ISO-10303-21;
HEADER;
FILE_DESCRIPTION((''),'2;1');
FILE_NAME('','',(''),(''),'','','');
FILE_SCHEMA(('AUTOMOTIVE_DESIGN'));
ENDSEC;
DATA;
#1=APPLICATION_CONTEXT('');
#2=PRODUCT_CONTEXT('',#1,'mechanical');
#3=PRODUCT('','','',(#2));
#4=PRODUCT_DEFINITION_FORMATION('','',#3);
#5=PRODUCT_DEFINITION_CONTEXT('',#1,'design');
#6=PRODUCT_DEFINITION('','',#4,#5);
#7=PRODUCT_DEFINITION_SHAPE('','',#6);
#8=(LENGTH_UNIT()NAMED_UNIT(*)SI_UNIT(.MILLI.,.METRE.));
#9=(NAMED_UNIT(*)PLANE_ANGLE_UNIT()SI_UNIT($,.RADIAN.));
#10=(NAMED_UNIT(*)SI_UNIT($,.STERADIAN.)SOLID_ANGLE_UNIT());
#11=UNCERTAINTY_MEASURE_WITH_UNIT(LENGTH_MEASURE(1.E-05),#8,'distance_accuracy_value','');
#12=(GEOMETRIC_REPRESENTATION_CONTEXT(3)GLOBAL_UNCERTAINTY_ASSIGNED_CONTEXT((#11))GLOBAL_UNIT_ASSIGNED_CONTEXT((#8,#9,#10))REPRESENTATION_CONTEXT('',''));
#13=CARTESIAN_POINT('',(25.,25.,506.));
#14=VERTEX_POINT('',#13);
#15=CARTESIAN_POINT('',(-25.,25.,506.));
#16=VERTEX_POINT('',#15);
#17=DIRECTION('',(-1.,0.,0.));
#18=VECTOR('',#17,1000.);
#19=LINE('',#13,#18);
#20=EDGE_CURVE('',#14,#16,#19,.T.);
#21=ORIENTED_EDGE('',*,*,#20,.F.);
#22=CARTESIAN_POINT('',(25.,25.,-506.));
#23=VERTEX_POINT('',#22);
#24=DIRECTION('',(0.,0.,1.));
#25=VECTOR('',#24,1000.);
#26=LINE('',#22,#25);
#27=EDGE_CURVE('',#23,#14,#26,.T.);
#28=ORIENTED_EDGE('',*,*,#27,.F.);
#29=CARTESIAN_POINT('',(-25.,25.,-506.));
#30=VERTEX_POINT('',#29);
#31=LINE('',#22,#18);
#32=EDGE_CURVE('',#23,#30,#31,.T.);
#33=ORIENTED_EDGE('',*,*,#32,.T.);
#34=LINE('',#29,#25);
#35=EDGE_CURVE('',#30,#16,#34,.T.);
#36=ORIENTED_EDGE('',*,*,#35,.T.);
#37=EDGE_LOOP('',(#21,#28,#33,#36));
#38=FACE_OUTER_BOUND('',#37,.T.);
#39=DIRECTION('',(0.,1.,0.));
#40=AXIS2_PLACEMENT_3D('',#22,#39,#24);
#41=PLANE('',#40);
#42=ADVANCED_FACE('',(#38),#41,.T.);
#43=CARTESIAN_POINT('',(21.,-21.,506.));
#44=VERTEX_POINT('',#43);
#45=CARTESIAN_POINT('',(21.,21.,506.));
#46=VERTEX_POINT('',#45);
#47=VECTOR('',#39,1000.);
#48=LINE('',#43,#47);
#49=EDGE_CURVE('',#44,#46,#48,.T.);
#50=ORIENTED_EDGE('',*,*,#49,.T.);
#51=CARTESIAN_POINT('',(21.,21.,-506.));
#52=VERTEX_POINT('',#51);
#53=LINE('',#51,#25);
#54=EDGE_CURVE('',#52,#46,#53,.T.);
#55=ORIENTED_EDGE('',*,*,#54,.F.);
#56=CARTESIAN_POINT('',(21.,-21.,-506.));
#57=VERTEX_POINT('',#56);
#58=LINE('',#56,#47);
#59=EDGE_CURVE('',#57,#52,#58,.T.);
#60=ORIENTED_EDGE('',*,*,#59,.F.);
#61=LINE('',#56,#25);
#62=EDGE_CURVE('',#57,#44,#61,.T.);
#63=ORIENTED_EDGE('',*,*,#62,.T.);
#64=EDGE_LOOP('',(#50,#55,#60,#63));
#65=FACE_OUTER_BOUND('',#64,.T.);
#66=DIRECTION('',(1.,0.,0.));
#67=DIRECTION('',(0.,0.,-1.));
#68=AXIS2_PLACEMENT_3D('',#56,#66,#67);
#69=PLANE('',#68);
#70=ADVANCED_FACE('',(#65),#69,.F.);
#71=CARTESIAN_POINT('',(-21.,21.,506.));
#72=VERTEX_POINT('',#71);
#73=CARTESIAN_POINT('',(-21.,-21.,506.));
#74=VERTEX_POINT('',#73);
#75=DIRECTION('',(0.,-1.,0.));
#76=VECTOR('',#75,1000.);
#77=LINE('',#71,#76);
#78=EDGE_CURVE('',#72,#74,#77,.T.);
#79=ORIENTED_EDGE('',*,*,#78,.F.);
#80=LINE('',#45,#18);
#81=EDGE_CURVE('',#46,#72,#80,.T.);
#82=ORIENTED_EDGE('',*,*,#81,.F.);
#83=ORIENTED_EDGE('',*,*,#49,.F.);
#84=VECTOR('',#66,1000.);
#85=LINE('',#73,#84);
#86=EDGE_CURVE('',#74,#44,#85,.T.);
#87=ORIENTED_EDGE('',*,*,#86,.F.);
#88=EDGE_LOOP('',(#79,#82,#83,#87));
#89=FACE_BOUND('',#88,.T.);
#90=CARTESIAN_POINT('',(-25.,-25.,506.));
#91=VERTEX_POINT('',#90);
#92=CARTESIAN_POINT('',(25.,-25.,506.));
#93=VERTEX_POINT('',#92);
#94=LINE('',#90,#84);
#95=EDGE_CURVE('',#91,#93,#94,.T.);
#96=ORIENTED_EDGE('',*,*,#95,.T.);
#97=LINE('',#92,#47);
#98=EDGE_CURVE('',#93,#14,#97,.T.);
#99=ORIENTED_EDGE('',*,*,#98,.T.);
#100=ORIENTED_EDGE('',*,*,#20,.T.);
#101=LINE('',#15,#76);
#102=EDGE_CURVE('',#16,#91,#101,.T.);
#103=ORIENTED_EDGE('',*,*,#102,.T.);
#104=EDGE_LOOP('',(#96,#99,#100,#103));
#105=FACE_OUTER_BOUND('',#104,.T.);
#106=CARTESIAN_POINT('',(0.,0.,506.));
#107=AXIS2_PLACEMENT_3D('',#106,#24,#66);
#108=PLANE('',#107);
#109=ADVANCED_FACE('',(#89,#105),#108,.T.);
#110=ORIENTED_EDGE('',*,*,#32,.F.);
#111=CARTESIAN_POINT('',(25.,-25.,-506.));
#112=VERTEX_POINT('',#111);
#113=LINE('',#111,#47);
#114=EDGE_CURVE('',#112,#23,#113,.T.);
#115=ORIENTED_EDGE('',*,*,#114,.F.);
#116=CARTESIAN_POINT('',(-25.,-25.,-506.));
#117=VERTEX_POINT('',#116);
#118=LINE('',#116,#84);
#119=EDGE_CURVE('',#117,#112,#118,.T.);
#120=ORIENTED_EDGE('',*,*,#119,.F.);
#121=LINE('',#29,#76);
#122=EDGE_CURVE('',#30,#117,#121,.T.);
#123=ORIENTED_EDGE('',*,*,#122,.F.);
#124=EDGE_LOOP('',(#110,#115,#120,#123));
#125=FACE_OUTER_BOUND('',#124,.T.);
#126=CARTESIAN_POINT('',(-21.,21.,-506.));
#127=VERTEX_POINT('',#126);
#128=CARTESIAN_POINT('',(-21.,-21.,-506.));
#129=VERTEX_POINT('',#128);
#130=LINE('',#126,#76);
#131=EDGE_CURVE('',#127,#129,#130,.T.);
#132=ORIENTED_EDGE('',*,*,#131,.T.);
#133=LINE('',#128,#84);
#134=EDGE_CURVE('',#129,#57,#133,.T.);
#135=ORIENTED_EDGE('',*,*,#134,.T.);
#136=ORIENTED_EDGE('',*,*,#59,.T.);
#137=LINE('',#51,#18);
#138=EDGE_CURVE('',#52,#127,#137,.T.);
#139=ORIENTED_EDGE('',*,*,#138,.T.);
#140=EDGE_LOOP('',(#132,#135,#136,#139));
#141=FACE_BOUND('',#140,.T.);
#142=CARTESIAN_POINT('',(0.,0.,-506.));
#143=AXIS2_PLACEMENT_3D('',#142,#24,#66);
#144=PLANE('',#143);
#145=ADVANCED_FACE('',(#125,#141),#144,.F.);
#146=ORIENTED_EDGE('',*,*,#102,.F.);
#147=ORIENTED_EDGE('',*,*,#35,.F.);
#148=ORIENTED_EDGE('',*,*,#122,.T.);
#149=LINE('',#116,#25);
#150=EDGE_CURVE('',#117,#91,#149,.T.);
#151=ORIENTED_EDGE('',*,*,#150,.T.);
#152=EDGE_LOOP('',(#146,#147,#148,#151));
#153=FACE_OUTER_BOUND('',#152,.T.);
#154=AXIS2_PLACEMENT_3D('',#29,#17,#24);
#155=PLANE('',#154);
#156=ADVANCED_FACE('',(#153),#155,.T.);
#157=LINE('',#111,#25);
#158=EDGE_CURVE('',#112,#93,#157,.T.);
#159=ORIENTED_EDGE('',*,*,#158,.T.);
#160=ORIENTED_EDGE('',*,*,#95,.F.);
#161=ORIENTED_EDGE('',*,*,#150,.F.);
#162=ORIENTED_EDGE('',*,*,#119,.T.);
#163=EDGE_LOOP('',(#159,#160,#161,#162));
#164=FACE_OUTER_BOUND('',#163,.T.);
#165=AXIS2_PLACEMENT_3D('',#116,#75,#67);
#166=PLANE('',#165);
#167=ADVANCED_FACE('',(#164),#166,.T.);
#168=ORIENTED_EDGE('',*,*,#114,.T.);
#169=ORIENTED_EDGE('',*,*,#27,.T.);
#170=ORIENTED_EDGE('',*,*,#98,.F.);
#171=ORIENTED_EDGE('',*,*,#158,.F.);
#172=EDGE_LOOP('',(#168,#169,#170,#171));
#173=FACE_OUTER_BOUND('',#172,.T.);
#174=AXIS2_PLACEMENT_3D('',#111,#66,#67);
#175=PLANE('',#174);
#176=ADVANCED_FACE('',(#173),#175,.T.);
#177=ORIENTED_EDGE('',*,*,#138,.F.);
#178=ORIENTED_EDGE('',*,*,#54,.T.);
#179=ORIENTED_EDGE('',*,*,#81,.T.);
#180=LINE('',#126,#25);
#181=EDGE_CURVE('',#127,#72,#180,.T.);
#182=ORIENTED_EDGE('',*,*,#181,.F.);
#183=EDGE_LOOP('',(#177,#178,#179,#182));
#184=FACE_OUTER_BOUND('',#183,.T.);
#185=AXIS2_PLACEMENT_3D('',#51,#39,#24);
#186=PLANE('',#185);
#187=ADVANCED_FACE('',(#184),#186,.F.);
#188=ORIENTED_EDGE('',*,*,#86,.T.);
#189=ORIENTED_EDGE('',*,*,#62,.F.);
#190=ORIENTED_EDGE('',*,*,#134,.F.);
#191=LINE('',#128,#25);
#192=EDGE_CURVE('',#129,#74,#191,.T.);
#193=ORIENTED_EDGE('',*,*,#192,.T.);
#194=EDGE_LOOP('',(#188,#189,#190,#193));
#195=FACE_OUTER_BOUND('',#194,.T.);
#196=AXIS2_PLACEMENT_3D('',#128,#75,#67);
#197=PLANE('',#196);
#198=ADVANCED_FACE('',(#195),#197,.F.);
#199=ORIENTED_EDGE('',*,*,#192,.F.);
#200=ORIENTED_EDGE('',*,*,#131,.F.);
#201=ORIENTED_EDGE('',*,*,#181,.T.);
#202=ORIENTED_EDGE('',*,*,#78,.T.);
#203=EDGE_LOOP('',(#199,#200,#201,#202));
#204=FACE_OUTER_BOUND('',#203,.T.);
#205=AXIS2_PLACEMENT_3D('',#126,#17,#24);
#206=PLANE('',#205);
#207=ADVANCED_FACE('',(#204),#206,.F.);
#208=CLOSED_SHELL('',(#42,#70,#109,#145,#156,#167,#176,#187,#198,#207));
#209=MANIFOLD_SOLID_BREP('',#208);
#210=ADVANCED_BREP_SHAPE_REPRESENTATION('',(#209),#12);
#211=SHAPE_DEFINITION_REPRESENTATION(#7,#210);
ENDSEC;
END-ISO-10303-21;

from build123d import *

# Parameters (mm, degrees)
SKETCH_1_W      = 50
SKETCH_1_H      = 50
SKETCH_1_W_2    = 42
SKETCH_1_H_2    = 42
EXTRUDE_1_DEPTH = 506


with BuildPart() as part:
    # 草图1 → 凸台-拉伸1 (new, symmetric)
    with BuildSketch(Plane.XY):
        Rectangle(SKETCH_1_W, SKETCH_1_H)
        Rectangle(SKETCH_1_W_2, SKETCH_1_H_2, mode=Mode.SUBTRACT)
    extrude(amount=EXTRUDE_1_DEPTH, both=True)


solid = part.part
